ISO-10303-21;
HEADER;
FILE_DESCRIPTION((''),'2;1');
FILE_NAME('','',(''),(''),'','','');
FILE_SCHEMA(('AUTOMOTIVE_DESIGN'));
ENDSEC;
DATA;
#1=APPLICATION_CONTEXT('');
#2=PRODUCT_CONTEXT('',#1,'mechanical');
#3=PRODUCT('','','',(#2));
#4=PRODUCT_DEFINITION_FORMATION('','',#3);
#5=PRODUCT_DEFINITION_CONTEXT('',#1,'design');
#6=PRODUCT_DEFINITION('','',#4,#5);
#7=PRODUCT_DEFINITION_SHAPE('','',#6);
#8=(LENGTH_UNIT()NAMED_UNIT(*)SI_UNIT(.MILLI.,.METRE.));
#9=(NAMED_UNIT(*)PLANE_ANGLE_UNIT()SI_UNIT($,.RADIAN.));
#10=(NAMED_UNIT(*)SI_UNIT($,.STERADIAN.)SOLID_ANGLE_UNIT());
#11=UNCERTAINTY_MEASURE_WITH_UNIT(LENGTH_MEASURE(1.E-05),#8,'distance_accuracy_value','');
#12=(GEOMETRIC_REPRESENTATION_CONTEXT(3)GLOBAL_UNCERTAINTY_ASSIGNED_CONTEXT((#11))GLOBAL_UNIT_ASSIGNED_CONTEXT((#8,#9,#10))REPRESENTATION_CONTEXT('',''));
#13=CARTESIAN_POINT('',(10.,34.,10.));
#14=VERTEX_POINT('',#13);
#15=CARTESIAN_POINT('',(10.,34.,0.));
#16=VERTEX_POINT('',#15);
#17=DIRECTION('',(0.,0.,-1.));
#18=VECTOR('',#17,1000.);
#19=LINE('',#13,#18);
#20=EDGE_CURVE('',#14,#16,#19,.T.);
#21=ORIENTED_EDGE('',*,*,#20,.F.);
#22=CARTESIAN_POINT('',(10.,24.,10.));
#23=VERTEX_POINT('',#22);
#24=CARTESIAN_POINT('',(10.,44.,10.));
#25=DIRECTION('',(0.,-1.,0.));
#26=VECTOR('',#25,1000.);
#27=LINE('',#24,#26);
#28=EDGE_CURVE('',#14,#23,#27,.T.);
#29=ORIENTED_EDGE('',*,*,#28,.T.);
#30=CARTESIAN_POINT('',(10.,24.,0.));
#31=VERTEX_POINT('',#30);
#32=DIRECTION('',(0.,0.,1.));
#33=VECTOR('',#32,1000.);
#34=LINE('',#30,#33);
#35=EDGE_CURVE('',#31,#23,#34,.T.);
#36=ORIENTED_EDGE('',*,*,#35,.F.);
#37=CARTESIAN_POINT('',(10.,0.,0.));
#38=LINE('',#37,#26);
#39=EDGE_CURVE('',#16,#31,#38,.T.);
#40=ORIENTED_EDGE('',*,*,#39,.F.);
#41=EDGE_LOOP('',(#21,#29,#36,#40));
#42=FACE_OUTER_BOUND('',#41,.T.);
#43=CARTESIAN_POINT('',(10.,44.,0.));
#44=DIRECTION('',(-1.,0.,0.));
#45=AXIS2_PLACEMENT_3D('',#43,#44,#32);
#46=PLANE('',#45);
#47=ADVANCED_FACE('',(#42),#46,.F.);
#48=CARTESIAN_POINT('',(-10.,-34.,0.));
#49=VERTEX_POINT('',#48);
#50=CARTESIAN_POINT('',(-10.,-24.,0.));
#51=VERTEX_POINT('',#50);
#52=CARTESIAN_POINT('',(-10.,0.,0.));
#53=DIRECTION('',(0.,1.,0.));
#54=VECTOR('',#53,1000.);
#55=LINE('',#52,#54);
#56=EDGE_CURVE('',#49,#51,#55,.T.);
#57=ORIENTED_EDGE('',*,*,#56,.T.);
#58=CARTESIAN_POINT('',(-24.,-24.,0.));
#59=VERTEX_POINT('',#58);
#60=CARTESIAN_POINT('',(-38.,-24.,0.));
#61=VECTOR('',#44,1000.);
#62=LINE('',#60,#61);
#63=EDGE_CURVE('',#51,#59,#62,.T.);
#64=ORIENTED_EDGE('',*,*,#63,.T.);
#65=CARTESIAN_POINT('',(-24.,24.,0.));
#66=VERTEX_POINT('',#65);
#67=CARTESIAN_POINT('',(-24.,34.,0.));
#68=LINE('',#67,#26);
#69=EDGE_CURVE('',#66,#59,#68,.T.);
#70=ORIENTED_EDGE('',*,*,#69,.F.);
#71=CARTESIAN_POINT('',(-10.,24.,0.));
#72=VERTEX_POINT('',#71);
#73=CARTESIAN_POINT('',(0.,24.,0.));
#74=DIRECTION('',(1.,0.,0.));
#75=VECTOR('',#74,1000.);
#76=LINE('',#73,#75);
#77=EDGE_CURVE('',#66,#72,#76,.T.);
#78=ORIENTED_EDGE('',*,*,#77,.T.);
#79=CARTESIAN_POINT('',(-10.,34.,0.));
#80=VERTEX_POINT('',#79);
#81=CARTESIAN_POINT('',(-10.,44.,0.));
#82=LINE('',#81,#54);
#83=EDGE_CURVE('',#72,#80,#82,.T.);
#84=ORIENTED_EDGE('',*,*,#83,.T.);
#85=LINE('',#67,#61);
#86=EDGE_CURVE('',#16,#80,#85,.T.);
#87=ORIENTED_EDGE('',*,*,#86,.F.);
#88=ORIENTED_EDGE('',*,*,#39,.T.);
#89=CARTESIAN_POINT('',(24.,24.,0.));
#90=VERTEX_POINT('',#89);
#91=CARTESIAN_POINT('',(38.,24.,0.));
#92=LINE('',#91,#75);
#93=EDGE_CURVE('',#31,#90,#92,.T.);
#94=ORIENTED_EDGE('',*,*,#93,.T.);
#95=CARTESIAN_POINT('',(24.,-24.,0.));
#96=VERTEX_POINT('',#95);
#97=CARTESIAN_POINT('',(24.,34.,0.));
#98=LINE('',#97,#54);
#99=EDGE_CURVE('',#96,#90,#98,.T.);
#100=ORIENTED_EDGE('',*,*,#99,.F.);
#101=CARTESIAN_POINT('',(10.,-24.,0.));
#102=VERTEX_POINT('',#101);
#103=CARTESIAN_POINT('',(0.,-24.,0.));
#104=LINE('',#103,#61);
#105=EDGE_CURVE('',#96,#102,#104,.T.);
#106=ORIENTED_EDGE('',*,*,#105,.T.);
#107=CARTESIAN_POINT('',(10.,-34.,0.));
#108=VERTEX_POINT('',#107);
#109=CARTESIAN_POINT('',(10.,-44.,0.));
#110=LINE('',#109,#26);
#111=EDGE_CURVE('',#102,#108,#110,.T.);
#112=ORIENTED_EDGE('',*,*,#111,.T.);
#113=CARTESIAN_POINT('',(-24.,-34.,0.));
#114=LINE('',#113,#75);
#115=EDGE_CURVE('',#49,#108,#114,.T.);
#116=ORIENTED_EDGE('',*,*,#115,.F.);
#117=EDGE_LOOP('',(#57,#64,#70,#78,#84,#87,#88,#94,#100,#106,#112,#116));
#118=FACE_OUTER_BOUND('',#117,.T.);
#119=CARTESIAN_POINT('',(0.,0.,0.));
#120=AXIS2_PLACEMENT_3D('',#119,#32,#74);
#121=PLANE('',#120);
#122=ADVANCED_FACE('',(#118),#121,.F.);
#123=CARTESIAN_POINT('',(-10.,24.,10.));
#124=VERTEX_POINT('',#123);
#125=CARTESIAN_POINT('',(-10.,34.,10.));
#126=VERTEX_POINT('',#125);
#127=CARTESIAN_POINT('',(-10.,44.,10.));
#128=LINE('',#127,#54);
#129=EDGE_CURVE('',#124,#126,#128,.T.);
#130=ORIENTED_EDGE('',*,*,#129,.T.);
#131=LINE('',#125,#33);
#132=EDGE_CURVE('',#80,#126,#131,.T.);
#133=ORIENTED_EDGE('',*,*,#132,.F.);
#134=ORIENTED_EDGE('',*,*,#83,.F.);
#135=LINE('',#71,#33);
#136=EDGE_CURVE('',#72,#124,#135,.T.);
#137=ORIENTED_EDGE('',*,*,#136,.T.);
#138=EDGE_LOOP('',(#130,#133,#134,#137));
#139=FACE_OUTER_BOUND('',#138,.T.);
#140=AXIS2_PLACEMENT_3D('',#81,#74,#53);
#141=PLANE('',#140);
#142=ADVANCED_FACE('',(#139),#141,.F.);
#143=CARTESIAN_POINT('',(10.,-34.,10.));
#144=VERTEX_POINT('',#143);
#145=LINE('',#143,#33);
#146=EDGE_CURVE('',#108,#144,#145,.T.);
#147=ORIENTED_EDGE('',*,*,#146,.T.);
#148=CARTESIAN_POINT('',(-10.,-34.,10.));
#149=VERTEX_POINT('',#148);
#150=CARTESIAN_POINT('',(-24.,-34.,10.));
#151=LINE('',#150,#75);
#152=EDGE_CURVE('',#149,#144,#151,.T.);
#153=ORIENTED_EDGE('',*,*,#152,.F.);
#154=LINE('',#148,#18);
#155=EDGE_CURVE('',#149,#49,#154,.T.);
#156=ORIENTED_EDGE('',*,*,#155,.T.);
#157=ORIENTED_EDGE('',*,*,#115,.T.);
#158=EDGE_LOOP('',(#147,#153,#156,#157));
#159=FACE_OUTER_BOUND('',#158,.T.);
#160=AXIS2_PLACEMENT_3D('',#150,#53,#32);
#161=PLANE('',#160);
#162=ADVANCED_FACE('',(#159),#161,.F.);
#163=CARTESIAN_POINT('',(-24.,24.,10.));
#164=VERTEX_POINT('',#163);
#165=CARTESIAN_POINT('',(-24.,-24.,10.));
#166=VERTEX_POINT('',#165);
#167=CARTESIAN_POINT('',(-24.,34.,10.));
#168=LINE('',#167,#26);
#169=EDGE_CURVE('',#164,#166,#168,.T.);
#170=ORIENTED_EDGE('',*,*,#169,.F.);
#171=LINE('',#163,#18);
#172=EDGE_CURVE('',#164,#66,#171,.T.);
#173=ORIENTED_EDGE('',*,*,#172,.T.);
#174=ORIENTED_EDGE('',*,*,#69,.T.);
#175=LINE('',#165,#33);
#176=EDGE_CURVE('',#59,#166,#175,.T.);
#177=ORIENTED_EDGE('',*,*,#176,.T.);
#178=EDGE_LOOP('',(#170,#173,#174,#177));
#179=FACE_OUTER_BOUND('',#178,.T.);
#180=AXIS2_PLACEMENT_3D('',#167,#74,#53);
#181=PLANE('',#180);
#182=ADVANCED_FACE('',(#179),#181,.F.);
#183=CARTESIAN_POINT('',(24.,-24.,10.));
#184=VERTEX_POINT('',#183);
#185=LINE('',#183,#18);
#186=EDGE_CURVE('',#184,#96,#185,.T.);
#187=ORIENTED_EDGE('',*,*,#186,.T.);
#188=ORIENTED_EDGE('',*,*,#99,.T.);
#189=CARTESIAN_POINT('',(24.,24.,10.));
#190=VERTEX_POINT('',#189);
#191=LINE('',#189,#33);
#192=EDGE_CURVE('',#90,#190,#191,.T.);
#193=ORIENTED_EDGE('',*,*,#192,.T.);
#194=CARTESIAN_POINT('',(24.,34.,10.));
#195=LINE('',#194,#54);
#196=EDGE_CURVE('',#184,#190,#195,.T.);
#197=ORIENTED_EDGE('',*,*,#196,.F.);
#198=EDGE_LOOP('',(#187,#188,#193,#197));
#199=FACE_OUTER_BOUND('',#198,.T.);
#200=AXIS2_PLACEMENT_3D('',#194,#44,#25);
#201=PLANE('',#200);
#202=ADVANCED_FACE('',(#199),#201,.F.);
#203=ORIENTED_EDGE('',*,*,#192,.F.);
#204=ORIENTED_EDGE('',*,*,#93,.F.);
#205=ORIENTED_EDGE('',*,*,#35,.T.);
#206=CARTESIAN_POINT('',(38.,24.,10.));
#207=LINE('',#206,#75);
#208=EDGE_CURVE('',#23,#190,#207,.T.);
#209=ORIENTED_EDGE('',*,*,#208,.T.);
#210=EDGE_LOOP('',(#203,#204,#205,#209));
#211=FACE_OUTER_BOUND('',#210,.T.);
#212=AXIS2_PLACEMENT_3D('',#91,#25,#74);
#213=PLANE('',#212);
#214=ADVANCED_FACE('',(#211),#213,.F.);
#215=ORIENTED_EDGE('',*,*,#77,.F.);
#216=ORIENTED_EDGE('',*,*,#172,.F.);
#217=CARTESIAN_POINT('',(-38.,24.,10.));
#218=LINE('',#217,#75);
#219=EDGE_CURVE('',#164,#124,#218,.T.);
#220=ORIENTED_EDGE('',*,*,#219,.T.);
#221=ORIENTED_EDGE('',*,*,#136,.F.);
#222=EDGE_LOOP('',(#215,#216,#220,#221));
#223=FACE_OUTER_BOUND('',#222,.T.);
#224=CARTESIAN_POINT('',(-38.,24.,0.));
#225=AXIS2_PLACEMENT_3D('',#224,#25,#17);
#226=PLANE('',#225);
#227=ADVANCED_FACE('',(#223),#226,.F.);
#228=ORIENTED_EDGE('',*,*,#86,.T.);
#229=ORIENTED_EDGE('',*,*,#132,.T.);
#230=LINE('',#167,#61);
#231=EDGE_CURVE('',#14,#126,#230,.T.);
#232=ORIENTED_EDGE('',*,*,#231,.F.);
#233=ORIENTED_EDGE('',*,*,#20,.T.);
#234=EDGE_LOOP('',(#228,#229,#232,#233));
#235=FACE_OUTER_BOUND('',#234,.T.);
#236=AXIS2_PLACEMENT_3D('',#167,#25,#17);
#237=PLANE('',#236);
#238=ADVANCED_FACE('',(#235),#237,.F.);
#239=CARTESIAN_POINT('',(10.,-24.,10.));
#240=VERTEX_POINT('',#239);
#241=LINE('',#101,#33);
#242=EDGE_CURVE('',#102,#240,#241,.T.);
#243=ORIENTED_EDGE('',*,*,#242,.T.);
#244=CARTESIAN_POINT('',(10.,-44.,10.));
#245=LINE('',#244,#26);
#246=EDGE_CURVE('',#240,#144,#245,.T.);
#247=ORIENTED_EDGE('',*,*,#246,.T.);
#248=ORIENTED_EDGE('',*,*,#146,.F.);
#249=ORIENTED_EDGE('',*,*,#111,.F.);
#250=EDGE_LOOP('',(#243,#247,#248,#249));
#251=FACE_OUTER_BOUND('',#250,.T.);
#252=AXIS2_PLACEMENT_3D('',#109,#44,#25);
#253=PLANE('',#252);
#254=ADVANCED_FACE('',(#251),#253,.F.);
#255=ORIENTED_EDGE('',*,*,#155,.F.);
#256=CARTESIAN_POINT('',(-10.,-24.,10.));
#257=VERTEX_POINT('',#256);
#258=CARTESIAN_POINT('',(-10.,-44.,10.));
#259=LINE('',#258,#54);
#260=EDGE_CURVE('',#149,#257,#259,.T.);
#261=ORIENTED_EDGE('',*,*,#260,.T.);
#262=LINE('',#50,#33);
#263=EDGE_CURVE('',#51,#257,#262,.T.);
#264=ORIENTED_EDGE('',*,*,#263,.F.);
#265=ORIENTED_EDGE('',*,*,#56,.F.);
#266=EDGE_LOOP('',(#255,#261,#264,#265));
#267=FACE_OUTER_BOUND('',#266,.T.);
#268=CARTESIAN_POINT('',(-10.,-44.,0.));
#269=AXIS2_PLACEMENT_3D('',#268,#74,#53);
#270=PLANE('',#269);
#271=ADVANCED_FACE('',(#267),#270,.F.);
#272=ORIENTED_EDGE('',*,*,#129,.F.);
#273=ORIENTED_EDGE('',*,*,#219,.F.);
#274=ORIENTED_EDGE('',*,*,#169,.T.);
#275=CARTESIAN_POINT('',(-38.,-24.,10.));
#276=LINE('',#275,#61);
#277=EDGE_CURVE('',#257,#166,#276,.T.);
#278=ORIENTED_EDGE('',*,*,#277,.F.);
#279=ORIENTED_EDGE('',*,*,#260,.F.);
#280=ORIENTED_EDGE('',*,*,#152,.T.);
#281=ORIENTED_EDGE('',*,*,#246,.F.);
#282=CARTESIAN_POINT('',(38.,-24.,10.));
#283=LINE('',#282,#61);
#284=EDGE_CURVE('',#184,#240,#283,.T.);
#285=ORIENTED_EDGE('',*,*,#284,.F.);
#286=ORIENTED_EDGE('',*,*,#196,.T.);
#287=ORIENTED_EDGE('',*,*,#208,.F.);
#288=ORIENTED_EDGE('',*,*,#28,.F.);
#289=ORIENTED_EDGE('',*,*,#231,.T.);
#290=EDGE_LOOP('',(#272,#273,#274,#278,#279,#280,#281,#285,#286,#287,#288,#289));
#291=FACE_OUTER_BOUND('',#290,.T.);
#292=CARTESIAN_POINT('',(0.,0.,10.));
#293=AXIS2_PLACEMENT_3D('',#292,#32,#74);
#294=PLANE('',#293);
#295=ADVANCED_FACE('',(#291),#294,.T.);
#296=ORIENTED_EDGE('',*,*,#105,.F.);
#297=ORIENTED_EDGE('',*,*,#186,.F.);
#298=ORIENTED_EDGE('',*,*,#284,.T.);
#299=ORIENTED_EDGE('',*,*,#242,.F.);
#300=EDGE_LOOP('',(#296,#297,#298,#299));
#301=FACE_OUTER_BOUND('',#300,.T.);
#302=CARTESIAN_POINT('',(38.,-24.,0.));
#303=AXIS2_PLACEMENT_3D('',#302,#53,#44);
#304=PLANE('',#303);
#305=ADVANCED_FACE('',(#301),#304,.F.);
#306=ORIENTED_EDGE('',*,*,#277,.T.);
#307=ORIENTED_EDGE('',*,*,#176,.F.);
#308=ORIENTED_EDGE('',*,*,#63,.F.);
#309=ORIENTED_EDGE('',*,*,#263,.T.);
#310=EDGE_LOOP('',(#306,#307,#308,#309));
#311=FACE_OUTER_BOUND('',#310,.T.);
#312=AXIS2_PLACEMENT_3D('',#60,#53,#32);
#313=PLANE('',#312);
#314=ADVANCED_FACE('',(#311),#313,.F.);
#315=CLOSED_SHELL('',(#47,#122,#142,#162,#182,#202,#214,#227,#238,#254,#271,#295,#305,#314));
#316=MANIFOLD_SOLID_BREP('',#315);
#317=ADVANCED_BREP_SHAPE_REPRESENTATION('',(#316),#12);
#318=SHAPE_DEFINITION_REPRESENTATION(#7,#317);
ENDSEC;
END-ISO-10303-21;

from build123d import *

# Parameters (mm, degrees)
SKETCH1_W           = 48
SKETCH1_H           = 68
BOSS_EXTRUDE1_DEPTH = 10
SKETCH2_W           = 28
SKETCH2_H           = 20
CUT_EXTRUDE1_DEPTH  = 10


with BuildPart() as part:
    # Sketch1 → Boss-Extrude1 (new body)
    with BuildSketch(Plane.XY):
        Rectangle(SKETCH1_W, SKETCH1_H)
    extrude(amount=BOSS_EXTRUDE1_DEPTH)

    # Sketch2 → Cut-Extrude1 (cut)
    with BuildSketch(Plane.XY.offset(10)):
        with Locations((-24, 34)):
            Rectangle(SKETCH2_W, SKETCH2_H)
        with Locations((24, 34)):
            Rectangle(SKETCH2_W, SKETCH2_H)
        with Locations((24, -34)):
            Rectangle(SKETCH2_W, SKETCH2_H)
        with Locations((-24, -34)):
            Rectangle(SKETCH2_W, SKETCH2_H)
    extrude(amount=-CUT_EXTRUDE1_DEPTH, mode=Mode.SUBTRACT)


solid = part.part
